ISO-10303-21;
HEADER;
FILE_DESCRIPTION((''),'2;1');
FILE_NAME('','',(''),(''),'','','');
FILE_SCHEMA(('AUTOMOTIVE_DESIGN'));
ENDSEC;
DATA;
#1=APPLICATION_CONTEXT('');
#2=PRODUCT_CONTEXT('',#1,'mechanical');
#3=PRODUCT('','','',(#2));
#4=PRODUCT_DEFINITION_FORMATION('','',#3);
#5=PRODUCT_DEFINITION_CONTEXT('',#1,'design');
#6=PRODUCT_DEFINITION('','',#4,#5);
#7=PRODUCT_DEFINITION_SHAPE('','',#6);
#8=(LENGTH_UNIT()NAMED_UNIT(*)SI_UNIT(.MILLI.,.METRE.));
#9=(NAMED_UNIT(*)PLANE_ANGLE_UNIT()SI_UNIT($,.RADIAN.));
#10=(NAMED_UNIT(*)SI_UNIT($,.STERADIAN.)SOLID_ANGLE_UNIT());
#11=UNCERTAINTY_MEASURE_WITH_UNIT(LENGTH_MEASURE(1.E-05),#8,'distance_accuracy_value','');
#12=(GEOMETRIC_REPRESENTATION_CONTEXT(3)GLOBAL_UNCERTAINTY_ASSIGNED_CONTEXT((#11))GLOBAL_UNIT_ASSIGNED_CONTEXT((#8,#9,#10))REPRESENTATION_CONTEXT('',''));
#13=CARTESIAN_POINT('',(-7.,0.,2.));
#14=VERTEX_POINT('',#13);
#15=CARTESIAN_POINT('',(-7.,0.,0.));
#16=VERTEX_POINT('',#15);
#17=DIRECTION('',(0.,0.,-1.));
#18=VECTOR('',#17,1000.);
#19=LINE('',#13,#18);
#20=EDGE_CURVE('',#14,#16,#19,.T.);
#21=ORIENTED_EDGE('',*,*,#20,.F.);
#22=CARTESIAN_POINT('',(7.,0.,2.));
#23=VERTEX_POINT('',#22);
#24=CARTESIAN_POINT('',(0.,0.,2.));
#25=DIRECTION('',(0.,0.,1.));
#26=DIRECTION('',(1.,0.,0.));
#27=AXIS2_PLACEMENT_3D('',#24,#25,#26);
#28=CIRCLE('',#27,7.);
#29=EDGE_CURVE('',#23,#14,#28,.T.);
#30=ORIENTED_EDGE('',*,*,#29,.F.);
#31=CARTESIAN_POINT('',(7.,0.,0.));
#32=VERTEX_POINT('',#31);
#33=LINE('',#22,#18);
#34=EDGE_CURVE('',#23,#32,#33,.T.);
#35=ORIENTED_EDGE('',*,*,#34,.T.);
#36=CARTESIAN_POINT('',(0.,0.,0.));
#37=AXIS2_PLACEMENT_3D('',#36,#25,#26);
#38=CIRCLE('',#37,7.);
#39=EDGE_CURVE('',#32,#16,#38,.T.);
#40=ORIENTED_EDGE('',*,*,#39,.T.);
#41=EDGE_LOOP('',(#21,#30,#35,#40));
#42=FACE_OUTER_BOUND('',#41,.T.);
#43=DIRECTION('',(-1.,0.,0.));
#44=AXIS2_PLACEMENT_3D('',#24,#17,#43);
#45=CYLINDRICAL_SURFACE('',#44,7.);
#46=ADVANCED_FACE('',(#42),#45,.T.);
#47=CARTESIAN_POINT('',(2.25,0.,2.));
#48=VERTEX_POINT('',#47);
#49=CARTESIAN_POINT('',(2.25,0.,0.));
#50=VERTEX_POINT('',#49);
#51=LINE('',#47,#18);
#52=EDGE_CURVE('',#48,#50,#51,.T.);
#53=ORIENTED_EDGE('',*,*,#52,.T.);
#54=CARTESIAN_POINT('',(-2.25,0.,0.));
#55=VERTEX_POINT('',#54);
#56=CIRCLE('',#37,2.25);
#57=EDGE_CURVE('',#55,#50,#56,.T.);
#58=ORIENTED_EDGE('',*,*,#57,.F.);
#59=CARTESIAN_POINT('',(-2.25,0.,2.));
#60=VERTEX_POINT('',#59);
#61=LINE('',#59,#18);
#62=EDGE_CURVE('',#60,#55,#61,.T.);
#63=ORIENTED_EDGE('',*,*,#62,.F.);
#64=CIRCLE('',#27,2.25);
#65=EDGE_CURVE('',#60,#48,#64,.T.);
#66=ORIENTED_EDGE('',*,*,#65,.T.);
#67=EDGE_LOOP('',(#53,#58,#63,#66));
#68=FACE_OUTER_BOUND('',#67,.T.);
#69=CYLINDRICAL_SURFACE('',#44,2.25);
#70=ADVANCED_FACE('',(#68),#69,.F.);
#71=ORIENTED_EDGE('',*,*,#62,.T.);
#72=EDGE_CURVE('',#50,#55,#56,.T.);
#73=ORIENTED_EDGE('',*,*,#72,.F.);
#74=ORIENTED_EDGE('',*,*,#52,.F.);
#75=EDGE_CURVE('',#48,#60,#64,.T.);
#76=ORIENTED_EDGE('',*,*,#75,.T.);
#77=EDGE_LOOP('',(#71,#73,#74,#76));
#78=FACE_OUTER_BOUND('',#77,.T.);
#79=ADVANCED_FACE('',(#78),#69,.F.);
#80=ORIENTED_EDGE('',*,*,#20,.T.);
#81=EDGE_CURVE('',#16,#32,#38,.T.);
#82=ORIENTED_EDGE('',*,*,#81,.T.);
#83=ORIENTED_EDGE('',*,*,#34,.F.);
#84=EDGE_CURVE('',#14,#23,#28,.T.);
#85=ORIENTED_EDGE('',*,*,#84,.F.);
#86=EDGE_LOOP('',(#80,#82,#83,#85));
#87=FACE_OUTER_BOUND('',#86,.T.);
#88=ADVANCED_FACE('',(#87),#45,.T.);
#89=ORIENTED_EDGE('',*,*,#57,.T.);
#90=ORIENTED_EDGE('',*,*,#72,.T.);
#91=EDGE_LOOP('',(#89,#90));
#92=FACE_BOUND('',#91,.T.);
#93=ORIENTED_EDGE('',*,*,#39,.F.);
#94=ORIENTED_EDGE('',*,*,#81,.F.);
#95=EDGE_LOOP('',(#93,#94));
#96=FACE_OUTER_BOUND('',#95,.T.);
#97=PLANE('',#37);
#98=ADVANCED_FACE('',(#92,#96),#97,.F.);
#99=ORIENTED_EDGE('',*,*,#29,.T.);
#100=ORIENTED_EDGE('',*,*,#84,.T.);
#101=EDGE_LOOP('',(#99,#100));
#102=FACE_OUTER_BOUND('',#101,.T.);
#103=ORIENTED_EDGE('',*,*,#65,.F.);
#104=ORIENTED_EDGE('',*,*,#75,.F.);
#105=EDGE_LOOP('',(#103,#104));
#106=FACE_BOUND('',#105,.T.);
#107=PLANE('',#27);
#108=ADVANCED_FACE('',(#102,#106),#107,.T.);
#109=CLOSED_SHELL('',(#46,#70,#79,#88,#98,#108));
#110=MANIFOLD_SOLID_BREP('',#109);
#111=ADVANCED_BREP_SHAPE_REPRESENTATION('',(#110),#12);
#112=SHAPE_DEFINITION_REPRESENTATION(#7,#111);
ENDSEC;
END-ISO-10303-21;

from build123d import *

# Parameters (mm, degrees)
SKETCH1_R           = 7
SKETCH1_R_2         = 2.25
BOSS_EXTRUDE1_DEPTH = 2


with BuildPart() as part:
    # Sketch1 → Boss-Extrude1 (new body)
    with BuildSketch(Plane.XY):
        Circle(SKETCH1_R)
        Circle(SKETCH1_R_2, mode=Mode.SUBTRACT)
    extrude(amount=BOSS_EXTRUDE1_DEPTH)


solid = part.part
